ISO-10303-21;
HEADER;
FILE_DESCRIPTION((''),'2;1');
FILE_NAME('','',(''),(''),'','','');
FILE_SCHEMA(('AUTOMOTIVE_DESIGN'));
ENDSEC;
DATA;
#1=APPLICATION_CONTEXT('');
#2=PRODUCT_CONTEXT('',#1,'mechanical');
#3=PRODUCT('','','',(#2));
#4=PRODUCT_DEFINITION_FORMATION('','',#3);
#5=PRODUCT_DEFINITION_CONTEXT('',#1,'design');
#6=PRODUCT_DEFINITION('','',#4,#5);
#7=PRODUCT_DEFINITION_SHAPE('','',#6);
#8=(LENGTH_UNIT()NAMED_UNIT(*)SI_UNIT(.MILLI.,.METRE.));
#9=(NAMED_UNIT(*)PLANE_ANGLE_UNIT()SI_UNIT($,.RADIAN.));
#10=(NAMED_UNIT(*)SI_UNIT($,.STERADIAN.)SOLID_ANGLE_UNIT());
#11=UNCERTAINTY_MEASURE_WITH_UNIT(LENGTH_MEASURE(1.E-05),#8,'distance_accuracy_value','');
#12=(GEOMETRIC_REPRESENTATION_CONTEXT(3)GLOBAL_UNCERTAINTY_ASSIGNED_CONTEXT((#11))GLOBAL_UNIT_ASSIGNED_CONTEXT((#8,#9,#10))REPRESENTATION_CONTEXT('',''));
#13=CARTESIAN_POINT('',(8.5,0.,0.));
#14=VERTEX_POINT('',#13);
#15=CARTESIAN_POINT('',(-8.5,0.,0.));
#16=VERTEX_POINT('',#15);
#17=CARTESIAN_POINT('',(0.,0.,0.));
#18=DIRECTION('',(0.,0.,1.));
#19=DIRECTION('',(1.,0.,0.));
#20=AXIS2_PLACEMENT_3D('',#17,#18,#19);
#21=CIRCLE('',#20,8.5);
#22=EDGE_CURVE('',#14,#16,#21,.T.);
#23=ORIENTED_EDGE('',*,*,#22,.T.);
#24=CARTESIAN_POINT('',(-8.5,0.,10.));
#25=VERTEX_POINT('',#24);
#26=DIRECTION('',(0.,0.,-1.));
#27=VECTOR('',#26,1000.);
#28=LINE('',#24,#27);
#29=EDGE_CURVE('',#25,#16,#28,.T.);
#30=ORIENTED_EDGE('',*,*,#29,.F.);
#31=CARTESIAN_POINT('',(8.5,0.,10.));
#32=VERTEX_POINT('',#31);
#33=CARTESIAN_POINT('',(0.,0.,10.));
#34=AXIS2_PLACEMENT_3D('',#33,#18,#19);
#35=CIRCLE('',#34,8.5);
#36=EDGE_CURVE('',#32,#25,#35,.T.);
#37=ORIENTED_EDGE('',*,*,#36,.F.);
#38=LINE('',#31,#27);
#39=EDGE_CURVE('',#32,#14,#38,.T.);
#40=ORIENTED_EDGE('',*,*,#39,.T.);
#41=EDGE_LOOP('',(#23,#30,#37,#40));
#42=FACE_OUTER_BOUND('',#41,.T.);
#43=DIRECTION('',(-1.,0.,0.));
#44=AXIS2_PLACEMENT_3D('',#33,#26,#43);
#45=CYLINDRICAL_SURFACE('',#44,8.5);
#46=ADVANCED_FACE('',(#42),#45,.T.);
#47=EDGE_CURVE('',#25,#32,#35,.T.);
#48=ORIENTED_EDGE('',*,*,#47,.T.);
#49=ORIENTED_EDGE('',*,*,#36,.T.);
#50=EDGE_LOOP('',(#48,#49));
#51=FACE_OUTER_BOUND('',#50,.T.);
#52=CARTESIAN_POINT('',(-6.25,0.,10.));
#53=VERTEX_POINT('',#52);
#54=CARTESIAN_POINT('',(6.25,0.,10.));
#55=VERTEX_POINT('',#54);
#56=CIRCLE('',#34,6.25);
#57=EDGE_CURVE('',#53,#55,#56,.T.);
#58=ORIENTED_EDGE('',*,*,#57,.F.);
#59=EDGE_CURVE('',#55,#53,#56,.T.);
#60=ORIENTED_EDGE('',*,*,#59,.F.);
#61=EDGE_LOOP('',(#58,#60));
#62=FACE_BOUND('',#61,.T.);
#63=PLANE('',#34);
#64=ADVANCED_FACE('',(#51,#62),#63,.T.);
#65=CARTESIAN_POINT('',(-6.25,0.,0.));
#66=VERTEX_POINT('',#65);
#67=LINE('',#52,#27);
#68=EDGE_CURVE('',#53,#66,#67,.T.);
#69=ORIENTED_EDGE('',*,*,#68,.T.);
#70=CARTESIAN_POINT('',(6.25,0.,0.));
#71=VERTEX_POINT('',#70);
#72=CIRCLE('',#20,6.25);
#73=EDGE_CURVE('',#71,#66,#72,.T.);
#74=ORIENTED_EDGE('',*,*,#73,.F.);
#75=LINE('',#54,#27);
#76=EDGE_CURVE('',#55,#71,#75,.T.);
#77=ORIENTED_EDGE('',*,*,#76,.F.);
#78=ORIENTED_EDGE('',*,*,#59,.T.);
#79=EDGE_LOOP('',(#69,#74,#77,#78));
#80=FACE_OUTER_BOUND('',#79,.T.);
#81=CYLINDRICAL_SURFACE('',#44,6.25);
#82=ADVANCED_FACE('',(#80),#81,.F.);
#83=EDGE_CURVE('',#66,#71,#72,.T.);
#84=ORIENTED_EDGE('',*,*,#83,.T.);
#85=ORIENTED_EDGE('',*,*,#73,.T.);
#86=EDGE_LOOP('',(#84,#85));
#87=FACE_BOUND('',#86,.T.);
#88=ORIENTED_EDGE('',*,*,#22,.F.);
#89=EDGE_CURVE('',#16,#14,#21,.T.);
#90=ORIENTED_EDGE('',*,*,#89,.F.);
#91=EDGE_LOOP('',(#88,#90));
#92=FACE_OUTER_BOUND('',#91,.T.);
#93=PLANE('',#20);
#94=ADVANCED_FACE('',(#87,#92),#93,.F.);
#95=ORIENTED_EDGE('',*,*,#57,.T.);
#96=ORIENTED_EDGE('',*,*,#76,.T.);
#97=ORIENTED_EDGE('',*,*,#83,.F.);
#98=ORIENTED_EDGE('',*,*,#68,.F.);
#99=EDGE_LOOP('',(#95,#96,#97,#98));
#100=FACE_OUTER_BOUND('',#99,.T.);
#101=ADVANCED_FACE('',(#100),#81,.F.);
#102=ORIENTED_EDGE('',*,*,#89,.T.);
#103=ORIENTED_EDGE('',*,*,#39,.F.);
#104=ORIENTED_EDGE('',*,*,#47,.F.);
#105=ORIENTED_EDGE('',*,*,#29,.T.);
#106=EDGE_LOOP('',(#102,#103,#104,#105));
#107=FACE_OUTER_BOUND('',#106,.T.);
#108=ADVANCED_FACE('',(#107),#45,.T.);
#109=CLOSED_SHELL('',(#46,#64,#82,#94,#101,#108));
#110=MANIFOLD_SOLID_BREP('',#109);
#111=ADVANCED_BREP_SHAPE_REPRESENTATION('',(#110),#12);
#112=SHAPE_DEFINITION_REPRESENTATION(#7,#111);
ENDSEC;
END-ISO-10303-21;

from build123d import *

# Parameters (mm, degrees)
SKETCH_1_R      = 8.5
SKETCH_1_R_2    = 6.25
EXTRUDE_1_DEPTH = 10


with BuildPart() as part:
    # 草图1 → 凸台-拉伸1 (new body)
    with BuildSketch(Plane.XY):
        Circle(SKETCH_1_R)
        Circle(SKETCH_1_R_2, mode=Mode.SUBTRACT)
    extrude(amount=EXTRUDE_1_DEPTH)


solid = part.part
